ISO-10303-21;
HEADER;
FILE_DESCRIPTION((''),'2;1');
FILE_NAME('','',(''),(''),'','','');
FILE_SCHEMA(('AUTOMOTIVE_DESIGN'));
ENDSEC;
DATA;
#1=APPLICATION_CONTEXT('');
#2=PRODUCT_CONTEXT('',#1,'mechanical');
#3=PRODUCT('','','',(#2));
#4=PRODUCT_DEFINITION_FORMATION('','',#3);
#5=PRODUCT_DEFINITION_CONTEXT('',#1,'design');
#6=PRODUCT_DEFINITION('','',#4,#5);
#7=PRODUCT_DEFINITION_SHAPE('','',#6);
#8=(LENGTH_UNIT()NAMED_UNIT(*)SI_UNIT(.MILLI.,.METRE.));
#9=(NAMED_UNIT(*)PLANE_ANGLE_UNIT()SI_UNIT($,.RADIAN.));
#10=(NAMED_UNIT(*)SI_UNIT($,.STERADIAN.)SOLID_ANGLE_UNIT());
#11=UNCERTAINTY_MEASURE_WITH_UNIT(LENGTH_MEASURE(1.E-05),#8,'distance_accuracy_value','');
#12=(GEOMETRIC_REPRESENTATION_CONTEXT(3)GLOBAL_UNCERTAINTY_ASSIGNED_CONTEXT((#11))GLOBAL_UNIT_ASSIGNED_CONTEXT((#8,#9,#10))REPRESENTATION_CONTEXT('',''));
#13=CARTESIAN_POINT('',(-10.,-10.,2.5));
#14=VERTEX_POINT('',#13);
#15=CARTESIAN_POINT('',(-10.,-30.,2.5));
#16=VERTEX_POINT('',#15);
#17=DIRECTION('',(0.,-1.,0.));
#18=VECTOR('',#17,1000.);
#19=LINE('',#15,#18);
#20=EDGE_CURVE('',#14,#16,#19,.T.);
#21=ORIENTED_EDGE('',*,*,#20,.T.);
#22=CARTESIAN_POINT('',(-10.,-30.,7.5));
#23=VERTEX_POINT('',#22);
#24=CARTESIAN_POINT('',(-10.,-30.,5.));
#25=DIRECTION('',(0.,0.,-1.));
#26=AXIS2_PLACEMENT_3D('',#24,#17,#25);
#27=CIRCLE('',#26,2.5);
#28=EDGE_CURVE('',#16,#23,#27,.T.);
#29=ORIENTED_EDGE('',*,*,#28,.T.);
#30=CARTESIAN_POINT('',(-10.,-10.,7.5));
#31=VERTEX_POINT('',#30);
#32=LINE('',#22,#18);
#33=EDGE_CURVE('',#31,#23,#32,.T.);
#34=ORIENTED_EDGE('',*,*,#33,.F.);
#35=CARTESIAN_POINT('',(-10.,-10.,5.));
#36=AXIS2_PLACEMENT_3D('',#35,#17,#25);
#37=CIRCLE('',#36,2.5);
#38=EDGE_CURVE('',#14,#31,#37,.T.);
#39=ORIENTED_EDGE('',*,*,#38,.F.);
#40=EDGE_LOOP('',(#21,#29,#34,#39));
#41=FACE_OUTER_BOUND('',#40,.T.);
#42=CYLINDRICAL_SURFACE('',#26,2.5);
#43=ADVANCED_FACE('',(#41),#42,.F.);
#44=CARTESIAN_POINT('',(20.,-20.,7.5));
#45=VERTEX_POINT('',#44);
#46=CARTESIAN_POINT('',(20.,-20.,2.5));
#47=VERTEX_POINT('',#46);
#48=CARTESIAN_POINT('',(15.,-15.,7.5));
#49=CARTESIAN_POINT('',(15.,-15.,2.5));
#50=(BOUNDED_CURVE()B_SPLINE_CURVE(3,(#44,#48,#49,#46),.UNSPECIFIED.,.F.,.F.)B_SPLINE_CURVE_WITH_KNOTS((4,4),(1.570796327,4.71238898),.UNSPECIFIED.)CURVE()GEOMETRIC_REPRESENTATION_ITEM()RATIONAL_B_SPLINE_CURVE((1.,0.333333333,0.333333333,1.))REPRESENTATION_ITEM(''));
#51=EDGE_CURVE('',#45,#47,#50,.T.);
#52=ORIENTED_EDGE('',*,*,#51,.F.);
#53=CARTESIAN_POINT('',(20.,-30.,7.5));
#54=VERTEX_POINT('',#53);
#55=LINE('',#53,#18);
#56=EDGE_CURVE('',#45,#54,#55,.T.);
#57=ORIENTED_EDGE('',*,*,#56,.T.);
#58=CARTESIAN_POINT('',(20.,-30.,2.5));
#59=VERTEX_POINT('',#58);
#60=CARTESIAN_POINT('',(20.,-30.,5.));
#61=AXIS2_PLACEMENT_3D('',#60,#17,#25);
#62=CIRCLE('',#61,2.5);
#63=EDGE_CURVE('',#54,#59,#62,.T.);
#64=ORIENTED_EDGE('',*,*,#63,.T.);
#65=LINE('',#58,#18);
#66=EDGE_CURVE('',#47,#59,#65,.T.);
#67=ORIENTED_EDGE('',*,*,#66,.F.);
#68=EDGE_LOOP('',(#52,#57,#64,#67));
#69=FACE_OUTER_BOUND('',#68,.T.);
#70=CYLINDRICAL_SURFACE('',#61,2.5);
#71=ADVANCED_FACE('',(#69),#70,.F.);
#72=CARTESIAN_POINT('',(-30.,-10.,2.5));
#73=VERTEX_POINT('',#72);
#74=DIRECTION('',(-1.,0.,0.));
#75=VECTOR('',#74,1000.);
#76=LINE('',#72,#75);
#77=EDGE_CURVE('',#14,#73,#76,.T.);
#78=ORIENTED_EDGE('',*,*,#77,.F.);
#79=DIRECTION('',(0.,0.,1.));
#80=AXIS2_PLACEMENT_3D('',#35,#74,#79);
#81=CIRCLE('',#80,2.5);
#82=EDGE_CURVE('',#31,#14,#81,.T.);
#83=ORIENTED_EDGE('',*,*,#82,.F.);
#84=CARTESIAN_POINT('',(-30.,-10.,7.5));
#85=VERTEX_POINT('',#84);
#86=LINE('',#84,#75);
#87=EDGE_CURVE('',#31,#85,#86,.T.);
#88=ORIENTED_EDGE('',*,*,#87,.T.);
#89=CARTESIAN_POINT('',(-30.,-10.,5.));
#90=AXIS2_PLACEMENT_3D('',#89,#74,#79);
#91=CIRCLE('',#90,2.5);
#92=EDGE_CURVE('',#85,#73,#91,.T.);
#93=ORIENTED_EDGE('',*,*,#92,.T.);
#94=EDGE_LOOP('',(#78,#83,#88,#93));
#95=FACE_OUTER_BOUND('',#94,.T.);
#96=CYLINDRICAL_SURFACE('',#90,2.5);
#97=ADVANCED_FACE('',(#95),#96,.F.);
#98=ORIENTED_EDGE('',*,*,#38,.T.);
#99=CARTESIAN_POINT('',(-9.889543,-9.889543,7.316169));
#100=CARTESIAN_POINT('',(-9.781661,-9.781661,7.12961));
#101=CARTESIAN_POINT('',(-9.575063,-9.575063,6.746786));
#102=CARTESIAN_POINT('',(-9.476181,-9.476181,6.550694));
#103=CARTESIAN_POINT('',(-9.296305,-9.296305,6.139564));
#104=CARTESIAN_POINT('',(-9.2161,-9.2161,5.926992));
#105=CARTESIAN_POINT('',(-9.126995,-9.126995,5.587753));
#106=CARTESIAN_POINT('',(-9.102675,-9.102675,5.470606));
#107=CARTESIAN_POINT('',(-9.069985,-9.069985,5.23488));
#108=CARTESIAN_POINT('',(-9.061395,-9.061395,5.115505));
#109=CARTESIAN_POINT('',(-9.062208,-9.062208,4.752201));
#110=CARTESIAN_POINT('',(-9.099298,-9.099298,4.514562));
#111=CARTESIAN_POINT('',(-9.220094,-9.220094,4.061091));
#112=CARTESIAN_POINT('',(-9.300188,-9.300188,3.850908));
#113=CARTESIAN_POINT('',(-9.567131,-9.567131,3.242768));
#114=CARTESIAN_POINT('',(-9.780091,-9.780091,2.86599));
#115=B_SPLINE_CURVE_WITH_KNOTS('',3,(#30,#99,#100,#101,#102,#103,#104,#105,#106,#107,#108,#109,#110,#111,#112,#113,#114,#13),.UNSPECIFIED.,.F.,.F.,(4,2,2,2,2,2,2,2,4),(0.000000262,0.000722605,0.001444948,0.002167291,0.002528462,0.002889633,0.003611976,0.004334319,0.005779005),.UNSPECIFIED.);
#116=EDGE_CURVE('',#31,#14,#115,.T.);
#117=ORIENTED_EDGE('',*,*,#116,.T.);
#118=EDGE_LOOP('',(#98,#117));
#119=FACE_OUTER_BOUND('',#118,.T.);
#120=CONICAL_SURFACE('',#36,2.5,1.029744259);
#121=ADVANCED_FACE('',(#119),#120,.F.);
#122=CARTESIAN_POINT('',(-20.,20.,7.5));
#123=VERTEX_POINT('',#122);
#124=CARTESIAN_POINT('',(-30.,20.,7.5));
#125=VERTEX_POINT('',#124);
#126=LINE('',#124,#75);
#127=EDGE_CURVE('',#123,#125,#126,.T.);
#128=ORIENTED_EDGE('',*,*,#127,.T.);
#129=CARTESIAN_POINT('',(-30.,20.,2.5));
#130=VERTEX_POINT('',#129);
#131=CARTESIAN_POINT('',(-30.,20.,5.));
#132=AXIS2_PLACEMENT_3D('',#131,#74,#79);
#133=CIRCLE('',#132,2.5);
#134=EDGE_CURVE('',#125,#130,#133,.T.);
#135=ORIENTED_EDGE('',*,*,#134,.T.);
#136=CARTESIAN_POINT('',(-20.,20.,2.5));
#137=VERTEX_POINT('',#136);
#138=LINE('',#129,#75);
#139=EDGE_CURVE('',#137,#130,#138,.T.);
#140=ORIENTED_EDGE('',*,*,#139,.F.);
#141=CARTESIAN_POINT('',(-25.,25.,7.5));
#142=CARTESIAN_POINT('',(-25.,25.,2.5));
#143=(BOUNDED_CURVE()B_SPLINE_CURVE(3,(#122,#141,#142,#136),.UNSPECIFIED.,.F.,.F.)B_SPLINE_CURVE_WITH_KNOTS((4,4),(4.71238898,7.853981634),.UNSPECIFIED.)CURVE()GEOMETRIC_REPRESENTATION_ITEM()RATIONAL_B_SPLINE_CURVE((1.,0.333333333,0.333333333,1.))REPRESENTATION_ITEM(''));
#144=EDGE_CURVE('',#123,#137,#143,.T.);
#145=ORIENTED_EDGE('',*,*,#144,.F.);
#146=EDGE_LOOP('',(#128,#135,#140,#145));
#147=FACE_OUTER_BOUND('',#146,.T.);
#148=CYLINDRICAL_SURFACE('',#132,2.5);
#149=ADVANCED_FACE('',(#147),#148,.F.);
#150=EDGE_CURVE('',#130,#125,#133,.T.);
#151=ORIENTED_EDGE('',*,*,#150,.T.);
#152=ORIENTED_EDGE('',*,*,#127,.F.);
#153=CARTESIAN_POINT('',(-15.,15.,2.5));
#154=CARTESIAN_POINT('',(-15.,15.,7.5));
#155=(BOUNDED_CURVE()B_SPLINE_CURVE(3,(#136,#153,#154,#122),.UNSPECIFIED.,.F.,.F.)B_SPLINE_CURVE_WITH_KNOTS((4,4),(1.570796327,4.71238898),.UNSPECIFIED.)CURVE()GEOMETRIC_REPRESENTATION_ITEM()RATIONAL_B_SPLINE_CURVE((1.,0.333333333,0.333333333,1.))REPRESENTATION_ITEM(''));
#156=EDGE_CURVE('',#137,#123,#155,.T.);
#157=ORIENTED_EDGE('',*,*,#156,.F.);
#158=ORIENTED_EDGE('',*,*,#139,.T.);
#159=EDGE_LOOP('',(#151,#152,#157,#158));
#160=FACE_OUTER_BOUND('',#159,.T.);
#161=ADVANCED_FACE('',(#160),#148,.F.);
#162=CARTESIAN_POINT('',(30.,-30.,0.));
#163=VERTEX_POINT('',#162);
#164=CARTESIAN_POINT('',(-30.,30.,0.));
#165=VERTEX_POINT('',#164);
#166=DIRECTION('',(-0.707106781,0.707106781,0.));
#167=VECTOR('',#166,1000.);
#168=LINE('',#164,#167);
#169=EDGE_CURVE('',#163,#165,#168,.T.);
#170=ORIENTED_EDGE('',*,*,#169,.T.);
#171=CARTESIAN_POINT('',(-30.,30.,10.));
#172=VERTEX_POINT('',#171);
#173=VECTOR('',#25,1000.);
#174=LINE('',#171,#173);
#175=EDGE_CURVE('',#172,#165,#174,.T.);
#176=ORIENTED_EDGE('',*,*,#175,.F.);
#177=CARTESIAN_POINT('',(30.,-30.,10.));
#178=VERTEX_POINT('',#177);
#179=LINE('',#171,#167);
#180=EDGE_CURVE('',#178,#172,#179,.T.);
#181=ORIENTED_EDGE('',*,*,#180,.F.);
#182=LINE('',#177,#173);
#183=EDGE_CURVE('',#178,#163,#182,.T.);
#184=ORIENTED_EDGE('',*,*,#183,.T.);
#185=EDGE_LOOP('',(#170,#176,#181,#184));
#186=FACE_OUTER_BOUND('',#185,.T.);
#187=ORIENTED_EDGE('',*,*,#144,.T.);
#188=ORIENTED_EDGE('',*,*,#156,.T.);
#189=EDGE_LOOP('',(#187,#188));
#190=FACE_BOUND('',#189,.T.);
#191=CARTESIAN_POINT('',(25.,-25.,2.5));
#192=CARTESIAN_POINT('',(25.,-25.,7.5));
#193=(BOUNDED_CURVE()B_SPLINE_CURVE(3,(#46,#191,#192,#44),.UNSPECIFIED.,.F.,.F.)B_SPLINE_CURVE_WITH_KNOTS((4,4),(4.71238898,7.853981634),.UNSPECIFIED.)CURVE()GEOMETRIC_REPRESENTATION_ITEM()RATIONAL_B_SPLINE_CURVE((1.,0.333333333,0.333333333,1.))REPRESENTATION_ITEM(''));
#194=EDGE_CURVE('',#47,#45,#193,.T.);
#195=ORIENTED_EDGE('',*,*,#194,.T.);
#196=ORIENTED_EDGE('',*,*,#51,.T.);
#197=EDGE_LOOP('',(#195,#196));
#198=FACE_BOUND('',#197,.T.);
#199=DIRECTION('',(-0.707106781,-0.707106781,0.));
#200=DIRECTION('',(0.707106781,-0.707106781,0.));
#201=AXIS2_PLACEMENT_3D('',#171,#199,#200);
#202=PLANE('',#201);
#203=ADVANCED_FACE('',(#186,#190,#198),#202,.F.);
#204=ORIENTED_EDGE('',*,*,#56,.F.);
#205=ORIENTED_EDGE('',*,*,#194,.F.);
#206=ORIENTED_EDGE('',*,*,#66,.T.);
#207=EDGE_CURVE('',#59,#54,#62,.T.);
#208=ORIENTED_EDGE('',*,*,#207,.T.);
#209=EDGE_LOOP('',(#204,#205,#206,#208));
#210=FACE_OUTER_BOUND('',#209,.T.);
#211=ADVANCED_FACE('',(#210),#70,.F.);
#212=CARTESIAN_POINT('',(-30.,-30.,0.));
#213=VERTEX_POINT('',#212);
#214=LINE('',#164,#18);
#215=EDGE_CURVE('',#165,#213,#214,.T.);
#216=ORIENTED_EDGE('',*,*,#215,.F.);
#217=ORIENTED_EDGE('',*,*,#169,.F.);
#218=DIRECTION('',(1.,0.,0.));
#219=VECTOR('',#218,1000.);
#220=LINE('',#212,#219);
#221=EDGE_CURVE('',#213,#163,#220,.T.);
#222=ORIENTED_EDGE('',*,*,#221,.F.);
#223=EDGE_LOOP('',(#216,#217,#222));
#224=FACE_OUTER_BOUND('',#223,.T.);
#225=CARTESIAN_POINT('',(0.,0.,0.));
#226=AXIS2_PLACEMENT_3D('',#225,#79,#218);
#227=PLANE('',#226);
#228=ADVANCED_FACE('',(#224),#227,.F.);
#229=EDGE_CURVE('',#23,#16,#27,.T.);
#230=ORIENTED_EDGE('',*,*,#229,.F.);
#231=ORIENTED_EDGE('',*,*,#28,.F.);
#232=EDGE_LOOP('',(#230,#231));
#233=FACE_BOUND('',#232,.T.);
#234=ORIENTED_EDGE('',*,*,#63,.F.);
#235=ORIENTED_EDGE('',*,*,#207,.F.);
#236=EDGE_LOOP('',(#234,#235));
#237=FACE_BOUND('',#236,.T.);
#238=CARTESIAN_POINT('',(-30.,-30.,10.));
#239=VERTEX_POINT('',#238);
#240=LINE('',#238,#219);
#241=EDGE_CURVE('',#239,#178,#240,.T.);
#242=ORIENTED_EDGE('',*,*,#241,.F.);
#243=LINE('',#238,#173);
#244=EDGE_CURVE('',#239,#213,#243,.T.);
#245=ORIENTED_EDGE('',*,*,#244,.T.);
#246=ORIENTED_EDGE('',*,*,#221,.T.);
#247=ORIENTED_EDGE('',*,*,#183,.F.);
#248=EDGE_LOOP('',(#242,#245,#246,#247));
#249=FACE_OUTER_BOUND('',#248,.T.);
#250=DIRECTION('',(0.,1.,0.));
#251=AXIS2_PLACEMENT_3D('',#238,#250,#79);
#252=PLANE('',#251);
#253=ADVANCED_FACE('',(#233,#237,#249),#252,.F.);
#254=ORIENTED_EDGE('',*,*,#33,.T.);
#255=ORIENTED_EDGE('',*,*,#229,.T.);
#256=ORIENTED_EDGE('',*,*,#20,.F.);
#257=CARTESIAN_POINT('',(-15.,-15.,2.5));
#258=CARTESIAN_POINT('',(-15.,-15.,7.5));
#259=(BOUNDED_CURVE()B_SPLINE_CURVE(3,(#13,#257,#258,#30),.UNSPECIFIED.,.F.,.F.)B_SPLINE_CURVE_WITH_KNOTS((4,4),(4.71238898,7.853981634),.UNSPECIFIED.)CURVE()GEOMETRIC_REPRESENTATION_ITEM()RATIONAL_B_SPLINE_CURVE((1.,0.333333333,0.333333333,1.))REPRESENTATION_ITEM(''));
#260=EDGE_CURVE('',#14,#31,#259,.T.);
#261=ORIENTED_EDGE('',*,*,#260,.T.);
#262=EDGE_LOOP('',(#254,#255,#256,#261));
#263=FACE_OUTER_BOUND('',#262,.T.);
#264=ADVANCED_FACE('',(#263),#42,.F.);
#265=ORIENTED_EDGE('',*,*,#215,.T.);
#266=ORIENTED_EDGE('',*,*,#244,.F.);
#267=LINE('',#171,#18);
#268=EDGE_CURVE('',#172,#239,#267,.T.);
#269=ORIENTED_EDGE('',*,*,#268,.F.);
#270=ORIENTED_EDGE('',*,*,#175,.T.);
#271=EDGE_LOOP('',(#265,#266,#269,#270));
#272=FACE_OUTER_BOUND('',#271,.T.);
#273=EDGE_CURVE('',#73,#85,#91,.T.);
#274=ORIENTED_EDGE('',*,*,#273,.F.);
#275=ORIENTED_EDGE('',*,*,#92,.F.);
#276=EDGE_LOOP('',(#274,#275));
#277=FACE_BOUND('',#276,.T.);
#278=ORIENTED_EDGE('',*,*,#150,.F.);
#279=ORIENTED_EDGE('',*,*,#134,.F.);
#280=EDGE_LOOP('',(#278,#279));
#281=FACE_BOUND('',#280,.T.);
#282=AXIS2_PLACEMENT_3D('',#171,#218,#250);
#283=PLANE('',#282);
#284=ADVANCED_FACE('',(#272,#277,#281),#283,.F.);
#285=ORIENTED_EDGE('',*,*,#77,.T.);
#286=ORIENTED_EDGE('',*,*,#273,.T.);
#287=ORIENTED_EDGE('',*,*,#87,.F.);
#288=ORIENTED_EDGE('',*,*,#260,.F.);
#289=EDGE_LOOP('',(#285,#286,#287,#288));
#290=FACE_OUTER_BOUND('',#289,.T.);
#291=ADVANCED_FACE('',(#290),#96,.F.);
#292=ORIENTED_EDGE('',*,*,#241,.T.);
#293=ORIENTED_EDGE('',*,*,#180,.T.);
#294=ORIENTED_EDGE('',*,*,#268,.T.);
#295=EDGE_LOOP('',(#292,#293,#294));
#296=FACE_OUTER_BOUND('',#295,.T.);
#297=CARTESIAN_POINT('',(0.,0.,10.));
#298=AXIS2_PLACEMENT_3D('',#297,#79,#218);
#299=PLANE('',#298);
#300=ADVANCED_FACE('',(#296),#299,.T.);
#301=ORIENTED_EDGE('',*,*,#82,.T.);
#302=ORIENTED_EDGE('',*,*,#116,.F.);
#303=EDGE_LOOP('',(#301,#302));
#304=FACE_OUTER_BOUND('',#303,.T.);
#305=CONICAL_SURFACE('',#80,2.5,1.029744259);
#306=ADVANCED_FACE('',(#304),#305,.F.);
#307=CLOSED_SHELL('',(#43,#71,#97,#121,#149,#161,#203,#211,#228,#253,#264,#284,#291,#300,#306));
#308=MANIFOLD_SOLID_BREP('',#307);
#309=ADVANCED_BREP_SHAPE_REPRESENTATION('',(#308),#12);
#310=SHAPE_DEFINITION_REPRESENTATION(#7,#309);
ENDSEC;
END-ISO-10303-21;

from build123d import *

# Parameters (mm, degrees)
EXTRUDE_1_DEPTH        = 10
HOLE_WIZARD_M6_2_D     = 5
HOLE_WIZARD_M6_2_DEPTH = 20
HOLE_WIZARD_M6_2_TIP   = 1.502151548
HOLE_WIZARD_M6_1_D     = 5
HOLE_WIZARD_M6_1_DEPTH = 20
HOLE_WIZARD_M6_1_TIP   = 1.502151548


with BuildPart() as part:
    # 草图1 → 凸台-拉伸1 (new body)
    with BuildSketch(Plane.XY):
        Polygon((-30, 30), (-30, -30), (30, -30), align=None)
    extrude(amount=EXTRUDE_1_DEPTH)

    # M6 螺纹孔2
    with Locations(Plane(origin=(0, -30, 0), x_dir=(-1, 0, 0), z_dir=(0, -1, 0))):
        with Locations((10, -5), (-20, -5)):
            Hole(HOLE_WIZARD_M6_2_D / 2, depth=HOLE_WIZARD_M6_2_DEPTH)
            with Locations((0, 0, -(HOLE_WIZARD_M6_2_DEPTH + HOLE_WIZARD_M6_2_TIP / 2))):  # 118° drill point
                Cone(0, HOLE_WIZARD_M6_2_D / 2, HOLE_WIZARD_M6_2_TIP, mode=Mode.SUBTRACT)

    # M6 螺纹孔1
    with Locations(Plane.ZY.offset(30)):
        with Locations((5, 20), (5, -10)):
            Hole(HOLE_WIZARD_M6_1_D / 2, depth=HOLE_WIZARD_M6_1_DEPTH)
            with Locations((0, 0, -(HOLE_WIZARD_M6_1_DEPTH + HOLE_WIZARD_M6_1_TIP / 2))):  # 118° drill point
                Cone(0, HOLE_WIZARD_M6_1_D / 2, HOLE_WIZARD_M6_1_TIP, mode=Mode.SUBTRACT)


solid = part.part
